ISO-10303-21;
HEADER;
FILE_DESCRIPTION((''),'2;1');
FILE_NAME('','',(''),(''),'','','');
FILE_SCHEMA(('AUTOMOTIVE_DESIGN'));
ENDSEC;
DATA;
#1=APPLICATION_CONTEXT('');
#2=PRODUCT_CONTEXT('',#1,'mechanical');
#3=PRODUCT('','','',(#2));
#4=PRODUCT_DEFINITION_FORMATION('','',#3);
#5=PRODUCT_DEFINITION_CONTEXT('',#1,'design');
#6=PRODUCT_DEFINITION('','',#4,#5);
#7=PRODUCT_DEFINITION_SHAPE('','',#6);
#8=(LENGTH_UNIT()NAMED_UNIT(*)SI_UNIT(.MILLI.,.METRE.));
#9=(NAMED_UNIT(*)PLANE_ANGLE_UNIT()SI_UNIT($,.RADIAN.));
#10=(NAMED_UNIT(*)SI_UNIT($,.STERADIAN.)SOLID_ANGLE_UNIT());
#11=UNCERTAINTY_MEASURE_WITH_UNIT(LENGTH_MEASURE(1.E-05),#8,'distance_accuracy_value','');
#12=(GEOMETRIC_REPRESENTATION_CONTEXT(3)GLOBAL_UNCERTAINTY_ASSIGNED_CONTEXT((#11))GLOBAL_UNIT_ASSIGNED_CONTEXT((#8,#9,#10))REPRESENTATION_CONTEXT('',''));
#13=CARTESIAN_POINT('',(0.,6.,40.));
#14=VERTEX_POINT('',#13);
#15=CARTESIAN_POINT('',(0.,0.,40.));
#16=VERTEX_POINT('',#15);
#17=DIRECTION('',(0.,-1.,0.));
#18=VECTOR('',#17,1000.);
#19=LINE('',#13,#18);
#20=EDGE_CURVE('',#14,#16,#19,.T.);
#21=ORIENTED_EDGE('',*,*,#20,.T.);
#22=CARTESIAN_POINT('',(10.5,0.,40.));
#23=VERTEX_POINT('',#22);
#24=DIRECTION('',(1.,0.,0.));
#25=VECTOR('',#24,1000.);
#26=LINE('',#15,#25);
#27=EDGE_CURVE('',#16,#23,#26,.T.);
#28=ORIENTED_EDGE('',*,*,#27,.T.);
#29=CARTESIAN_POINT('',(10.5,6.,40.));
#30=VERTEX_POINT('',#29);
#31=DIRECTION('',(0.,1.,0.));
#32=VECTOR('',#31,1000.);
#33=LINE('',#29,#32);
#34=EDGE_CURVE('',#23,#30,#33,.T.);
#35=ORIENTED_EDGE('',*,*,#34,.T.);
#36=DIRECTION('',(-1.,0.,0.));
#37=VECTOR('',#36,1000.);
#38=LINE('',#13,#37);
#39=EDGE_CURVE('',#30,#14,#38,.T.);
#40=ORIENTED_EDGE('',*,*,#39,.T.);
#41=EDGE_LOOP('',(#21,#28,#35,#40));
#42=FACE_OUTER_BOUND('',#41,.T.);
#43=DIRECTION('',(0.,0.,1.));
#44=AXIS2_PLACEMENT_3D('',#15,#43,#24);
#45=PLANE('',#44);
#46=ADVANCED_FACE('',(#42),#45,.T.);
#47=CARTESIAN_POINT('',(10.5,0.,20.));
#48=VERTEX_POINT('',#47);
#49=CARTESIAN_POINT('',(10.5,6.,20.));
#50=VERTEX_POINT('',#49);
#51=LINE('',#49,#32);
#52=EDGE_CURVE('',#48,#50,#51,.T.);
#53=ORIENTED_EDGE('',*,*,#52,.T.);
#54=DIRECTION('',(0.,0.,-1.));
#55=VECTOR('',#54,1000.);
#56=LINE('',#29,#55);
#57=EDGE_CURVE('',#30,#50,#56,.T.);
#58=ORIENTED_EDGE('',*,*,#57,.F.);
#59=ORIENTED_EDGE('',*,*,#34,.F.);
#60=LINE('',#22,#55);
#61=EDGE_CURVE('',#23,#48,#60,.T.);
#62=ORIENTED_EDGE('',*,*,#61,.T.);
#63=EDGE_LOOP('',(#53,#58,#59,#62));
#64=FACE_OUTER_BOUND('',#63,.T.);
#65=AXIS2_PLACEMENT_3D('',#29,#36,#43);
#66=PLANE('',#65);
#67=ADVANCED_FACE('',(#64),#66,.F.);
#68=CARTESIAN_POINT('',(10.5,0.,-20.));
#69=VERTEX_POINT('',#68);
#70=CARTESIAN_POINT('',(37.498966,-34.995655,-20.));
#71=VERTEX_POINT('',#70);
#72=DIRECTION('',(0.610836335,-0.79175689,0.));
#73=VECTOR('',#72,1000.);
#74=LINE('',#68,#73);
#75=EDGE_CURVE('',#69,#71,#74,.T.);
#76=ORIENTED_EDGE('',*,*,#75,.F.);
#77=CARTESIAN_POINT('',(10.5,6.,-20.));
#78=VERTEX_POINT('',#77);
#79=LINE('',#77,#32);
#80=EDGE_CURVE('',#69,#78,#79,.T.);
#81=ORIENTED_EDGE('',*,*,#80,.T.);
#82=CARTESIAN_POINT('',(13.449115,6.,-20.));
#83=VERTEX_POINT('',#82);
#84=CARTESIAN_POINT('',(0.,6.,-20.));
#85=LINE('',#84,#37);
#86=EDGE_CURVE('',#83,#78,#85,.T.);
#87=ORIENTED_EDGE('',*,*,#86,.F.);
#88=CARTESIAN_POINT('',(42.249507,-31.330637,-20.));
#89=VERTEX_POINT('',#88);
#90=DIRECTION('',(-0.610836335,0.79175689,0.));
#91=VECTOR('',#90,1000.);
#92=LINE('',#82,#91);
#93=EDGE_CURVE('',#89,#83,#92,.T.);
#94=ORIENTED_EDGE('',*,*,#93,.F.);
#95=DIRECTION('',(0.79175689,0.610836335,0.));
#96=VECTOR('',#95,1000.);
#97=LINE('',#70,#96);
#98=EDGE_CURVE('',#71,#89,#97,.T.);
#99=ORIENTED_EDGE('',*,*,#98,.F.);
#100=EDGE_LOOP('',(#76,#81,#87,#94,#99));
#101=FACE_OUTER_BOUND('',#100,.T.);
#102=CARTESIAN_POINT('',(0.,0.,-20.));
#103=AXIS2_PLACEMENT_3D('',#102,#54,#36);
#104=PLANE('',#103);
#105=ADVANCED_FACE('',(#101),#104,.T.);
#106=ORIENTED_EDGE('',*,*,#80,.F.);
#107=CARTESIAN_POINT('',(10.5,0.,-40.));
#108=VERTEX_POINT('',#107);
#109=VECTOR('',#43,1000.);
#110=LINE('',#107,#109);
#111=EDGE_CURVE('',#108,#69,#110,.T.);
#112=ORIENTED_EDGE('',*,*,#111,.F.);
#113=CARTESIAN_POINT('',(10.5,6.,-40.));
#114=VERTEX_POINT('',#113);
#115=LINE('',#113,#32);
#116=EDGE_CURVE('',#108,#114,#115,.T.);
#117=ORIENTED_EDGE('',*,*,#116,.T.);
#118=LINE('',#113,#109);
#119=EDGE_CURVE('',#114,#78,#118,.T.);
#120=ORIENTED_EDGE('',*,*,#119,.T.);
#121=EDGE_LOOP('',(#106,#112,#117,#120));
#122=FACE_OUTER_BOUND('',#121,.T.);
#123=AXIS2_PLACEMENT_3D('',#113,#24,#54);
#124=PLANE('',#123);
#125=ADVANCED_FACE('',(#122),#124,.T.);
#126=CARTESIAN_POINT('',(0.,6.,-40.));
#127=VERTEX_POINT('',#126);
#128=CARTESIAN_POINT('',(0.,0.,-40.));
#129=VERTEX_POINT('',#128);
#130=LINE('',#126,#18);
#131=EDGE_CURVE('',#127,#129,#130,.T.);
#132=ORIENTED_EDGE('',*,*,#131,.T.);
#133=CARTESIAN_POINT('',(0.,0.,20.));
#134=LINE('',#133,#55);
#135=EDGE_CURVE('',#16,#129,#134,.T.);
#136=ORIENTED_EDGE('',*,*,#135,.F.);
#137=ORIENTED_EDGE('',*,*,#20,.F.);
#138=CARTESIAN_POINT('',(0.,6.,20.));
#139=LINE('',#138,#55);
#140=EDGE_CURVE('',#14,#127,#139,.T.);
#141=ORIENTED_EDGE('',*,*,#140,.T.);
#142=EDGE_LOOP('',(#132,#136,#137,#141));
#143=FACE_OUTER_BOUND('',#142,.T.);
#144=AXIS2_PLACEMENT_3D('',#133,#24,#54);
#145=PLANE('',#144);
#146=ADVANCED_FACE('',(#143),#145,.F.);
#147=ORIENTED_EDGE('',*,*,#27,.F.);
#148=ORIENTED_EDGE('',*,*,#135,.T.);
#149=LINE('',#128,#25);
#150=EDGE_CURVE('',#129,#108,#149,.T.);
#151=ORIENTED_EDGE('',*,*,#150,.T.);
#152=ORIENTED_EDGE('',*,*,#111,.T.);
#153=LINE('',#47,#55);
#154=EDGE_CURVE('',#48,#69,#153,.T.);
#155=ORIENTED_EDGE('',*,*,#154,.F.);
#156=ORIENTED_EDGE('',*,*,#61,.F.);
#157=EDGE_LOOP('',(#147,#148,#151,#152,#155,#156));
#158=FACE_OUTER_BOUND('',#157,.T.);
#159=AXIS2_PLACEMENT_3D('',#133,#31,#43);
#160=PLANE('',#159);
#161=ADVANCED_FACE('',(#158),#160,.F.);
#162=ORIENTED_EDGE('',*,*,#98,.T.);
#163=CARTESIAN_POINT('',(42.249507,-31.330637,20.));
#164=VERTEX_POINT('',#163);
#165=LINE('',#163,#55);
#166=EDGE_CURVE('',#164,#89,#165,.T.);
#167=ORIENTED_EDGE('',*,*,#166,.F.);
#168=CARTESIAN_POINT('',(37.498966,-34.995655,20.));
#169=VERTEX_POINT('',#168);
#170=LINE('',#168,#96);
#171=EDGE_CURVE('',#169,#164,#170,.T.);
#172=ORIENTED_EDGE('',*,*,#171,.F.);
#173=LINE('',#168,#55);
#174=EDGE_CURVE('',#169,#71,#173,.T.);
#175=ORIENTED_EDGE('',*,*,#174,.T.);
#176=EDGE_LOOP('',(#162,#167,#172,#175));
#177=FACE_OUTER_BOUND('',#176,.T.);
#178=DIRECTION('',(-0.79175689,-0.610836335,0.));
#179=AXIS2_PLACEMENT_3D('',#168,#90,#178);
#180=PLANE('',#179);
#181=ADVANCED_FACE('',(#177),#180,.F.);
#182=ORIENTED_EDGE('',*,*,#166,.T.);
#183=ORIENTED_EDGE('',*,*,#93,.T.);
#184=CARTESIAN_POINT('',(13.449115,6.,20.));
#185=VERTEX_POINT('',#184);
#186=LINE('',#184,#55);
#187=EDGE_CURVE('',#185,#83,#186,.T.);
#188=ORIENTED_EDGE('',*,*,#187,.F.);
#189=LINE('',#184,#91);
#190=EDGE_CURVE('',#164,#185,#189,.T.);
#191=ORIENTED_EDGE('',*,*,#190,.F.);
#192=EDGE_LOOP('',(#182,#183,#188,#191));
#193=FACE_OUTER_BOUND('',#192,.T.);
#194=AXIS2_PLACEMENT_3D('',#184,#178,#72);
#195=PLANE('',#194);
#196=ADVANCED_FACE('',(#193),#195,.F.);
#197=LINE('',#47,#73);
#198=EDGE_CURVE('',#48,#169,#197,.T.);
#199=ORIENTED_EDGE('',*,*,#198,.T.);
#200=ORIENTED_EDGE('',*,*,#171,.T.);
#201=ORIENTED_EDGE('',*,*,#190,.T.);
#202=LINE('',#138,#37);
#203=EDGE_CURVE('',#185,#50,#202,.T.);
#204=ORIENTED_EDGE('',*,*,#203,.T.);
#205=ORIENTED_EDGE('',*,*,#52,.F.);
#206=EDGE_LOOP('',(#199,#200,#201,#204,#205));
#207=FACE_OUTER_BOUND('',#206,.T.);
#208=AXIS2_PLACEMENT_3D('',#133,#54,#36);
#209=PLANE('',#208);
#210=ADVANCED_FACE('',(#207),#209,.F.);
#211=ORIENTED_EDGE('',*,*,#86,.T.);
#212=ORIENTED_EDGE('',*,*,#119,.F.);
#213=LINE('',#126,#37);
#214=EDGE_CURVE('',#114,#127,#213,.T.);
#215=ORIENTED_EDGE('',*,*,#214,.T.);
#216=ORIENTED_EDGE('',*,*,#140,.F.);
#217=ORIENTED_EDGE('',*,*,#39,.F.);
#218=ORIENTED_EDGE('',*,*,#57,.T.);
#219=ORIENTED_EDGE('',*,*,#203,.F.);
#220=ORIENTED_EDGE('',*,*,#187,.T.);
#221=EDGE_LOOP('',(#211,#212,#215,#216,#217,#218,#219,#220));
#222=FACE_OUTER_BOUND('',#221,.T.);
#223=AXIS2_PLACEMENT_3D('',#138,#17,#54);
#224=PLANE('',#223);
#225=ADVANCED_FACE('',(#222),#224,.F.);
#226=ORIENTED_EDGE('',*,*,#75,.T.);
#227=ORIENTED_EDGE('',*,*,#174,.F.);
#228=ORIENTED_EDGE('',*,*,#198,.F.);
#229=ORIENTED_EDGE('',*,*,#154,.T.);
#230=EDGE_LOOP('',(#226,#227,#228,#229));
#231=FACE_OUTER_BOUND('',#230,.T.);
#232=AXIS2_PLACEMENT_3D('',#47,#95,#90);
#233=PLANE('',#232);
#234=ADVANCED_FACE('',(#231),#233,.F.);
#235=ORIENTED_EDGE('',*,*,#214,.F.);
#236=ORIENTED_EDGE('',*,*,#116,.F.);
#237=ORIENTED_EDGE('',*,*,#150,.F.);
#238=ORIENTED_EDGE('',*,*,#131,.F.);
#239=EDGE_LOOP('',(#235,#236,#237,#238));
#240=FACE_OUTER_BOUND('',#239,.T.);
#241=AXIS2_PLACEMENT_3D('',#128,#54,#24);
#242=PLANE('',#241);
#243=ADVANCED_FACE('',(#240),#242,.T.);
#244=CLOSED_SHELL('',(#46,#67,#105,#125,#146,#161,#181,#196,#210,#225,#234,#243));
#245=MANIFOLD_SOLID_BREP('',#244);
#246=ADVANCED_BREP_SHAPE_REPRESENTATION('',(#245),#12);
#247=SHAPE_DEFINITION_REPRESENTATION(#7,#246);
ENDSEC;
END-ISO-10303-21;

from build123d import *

# Parameters (mm, degrees)
BOSS_EXTRUDE2_DEPTH = 20
SKETCH4_W           = 10.5
SKETCH4_H           = 6
BOSS_EXTRUDE3_DEPTH = 20


with BuildPart() as part:
    # Sketch3 → Boss-Extrude2 (new, symmetric)
    with BuildSketch(Plane.XY):
        Polygon((0, 0), (10.5, 0), (37.498965991, -34.995654522), (42.249507329, -31.330636514), (13.449114839, 6), (0, 6), align=None)
    extrude(amount=BOSS_EXTRUDE2_DEPTH, both=True)

    # Sketch4 → Boss-Extrude3 (add)
    with BuildSketch(Plane.XY.offset(20)):
        with Locations((5.25, 3)):
            Rectangle(SKETCH4_W, SKETCH4_H)
    boss_extrude3 = extrude(amount=BOSS_EXTRUDE3_DEPTH)

    # Mirror1: Boss-Extrude3 across plane
    add(boss_extrude3.mirror(Plane.XY))


solid = part.part
